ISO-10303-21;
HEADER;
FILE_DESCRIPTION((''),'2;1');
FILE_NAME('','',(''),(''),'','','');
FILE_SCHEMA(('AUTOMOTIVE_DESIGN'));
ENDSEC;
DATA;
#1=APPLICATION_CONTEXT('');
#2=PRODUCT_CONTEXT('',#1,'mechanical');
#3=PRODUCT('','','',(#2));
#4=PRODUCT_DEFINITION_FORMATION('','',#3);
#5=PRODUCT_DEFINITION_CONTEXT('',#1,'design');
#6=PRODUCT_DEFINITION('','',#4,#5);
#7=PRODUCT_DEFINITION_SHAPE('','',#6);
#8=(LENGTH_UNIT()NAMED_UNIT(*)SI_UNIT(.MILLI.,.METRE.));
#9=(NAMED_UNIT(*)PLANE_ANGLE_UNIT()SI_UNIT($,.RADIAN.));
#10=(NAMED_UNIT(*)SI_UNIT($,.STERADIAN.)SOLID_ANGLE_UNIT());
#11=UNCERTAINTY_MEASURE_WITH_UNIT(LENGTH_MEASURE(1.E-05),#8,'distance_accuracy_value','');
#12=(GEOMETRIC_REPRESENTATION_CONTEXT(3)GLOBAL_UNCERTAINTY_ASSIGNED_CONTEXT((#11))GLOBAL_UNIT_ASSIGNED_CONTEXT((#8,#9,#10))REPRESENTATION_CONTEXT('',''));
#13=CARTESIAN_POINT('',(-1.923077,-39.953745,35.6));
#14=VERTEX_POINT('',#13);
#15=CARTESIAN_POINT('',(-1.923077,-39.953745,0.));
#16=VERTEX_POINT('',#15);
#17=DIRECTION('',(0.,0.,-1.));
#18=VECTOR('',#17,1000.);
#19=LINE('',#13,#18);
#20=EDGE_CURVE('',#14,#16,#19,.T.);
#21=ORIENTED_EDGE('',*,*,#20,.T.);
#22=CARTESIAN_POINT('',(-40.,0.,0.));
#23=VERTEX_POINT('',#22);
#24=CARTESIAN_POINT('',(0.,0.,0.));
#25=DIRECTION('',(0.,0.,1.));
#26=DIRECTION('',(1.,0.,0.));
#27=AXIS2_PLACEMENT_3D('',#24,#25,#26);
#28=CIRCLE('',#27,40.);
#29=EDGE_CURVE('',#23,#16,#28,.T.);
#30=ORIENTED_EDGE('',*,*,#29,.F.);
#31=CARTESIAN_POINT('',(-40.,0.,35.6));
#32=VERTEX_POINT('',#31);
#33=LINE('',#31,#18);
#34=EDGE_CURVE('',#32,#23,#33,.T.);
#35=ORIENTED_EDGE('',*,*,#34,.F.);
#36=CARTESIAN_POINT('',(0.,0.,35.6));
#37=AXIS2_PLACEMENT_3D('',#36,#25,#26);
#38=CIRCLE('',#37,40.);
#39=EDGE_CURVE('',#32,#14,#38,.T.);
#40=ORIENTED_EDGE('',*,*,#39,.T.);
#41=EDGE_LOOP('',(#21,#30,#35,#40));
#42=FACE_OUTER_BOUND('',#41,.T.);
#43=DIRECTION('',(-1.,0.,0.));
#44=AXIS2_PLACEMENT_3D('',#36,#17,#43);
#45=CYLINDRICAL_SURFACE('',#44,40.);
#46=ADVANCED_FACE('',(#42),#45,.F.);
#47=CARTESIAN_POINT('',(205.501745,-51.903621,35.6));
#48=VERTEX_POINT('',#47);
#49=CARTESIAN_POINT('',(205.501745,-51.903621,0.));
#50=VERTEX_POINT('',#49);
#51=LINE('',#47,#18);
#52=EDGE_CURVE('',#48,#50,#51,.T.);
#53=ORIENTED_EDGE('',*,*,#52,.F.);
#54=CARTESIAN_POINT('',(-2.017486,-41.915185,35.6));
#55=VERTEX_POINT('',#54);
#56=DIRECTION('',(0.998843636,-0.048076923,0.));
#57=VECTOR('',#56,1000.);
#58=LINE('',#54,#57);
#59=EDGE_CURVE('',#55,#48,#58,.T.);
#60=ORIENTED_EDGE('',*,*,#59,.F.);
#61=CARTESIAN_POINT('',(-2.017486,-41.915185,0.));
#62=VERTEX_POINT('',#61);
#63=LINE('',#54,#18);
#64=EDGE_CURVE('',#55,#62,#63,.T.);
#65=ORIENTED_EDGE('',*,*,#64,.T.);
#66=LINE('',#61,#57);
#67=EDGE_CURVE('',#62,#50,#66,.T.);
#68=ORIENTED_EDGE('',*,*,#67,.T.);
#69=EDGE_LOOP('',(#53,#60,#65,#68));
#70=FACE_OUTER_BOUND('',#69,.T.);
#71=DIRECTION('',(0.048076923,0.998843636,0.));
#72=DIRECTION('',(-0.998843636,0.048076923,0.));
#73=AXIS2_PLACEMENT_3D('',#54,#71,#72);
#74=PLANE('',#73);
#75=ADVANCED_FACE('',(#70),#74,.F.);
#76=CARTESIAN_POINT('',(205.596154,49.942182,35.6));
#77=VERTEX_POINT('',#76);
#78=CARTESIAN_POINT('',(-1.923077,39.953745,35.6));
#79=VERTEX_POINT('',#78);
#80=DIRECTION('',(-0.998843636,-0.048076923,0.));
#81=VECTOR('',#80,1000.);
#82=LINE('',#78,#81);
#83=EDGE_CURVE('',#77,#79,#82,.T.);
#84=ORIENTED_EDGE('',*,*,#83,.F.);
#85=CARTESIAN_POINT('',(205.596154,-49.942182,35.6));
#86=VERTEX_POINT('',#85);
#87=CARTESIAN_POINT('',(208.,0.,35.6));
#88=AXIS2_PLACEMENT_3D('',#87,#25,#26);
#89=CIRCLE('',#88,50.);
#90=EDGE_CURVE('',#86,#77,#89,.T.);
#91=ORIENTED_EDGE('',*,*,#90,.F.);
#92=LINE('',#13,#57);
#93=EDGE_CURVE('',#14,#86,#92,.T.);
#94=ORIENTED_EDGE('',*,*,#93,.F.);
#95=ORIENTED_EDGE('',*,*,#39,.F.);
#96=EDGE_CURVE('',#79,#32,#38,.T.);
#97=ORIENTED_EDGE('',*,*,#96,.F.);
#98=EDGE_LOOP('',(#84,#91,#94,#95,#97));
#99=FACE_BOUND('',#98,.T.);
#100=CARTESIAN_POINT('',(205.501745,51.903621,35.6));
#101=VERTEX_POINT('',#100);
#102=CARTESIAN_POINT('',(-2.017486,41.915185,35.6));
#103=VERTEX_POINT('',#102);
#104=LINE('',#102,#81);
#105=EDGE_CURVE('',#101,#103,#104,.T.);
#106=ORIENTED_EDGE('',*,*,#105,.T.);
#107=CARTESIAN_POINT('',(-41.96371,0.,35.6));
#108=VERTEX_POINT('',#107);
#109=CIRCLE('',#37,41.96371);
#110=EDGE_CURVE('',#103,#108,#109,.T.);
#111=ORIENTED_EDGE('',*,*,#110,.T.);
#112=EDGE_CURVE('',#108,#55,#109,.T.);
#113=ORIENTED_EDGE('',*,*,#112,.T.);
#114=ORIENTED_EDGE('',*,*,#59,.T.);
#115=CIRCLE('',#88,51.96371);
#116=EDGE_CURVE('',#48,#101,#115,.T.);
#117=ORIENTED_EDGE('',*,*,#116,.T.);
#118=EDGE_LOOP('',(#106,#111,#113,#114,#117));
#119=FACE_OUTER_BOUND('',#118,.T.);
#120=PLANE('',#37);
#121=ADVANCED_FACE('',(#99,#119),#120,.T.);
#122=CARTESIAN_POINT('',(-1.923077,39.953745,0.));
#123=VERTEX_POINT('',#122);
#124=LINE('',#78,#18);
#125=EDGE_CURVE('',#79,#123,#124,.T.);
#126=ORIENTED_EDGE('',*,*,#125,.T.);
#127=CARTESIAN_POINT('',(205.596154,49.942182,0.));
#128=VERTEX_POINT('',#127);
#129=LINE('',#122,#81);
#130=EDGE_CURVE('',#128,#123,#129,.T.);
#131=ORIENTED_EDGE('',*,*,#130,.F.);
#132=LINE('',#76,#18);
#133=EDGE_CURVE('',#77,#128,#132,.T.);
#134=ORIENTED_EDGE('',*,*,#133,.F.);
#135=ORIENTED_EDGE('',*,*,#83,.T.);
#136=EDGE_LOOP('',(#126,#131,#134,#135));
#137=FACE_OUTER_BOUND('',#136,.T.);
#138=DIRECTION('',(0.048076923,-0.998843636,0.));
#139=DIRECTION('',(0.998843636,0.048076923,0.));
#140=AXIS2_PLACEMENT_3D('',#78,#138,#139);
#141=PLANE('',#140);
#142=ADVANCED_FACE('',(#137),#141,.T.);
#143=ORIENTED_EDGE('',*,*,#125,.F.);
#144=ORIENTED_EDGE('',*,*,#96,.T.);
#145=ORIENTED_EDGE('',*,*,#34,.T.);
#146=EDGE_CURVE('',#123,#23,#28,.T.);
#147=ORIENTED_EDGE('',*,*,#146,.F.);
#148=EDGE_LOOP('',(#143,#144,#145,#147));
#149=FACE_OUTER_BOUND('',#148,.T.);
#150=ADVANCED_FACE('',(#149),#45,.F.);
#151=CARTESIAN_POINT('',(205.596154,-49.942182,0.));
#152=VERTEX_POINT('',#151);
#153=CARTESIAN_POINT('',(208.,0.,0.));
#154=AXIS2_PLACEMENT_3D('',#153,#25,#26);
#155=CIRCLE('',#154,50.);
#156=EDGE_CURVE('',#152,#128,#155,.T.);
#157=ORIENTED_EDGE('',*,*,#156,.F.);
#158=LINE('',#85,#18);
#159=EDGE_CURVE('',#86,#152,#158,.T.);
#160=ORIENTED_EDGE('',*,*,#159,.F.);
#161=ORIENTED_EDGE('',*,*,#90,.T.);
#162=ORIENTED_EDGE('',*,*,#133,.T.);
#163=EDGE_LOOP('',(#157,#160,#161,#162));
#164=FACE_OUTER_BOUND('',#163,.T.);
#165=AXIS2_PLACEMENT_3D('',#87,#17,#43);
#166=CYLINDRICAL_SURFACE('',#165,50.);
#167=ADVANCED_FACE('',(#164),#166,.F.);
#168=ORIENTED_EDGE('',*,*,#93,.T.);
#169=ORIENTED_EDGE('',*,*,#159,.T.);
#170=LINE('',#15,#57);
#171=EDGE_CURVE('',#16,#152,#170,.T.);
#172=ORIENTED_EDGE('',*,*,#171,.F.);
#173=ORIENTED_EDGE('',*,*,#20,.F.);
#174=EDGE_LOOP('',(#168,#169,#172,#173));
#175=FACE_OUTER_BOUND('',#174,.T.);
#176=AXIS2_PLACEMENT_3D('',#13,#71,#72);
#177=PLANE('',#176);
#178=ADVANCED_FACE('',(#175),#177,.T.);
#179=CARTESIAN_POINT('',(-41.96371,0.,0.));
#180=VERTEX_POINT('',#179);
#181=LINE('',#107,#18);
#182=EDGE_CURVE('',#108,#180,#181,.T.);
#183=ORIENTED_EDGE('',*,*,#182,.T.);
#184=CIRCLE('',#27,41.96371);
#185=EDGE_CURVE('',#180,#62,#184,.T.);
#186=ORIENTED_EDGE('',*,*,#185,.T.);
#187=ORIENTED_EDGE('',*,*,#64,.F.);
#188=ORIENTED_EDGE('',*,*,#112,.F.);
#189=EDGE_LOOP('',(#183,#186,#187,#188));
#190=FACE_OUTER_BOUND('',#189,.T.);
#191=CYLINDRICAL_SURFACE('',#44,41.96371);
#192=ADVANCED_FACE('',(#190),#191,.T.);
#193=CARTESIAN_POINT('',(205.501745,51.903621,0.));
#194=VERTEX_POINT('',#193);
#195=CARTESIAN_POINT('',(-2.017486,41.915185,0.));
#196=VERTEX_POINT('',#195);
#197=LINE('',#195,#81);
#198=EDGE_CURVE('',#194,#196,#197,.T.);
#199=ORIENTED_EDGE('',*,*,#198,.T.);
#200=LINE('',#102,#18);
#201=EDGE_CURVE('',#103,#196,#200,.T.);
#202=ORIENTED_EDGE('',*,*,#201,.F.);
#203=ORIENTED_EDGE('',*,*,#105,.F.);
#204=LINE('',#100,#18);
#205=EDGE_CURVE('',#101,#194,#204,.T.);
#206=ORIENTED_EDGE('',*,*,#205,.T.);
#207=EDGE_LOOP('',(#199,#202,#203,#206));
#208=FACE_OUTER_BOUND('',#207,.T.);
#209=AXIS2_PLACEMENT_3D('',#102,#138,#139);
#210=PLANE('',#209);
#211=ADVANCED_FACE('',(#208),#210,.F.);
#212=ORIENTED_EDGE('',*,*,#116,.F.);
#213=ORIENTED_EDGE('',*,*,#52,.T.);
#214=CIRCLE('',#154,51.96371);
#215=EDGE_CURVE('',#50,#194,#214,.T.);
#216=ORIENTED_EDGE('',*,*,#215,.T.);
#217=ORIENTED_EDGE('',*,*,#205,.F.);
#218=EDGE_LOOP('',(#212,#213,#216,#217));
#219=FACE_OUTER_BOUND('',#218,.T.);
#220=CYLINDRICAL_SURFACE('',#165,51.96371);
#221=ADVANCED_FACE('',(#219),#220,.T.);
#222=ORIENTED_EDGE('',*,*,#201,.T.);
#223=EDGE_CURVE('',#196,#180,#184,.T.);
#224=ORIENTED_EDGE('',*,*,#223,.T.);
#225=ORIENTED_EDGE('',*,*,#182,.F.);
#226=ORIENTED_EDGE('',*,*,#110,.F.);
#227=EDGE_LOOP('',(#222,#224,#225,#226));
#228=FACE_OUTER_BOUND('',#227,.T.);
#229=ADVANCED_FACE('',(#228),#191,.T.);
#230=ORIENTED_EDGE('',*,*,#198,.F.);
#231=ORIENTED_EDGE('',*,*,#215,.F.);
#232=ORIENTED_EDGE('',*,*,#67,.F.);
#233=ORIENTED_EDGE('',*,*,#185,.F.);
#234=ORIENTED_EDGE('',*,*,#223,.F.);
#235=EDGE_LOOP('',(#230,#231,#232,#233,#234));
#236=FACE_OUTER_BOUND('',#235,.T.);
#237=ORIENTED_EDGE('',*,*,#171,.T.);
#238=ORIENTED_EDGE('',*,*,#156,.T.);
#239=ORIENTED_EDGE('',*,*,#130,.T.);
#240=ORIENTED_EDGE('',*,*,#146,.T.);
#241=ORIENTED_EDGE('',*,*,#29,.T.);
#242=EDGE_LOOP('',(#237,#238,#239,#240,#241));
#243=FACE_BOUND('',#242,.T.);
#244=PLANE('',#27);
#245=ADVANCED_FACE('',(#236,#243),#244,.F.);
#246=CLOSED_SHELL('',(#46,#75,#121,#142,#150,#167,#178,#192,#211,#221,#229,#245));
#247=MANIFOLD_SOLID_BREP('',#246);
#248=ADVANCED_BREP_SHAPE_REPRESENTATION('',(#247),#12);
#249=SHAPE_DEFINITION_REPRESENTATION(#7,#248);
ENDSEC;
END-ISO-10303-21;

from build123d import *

# Parameters (mm, degrees)
BOSS_EXTRUDE1_DEPTH = 35.6


with BuildPart() as part:
    # Sketch1 → Boss-Extrude1 (new body)
    with BuildSketch(Plane.XY):
        with BuildLine():
            Line((-2.017486069, 41.915184916), (205.5017447, 51.903621277))
            ThreePointArc((205.5017447, 51.903621277), (259.963710234, 0), (205.5017447, -51.903621277))
            Line((205.5017447, -51.903621277), (-2.017486069, -41.915184916))
            ThreePointArc((-2.017486069, -41.915184916), (-41.963710234, 0), (-2.017486069, 41.915184916))
        make_face()
        with BuildLine():
            Line((-1.923076923, 39.953745446), (205.596153846, 49.942181807))
            ThreePointArc((205.596153846, 49.942181807), (258, 0), (205.596153846, -49.942181807))
            Line((205.596153846, -49.942181807), (-1.923076923, -39.953745446))
            ThreePointArc((-1.923076923, -39.953745446), (-40, 0), (-1.923076923, 39.953745446))
        make_face(mode=Mode.SUBTRACT)
    extrude(amount=BOSS_EXTRUDE1_DEPTH)


solid = part.part
